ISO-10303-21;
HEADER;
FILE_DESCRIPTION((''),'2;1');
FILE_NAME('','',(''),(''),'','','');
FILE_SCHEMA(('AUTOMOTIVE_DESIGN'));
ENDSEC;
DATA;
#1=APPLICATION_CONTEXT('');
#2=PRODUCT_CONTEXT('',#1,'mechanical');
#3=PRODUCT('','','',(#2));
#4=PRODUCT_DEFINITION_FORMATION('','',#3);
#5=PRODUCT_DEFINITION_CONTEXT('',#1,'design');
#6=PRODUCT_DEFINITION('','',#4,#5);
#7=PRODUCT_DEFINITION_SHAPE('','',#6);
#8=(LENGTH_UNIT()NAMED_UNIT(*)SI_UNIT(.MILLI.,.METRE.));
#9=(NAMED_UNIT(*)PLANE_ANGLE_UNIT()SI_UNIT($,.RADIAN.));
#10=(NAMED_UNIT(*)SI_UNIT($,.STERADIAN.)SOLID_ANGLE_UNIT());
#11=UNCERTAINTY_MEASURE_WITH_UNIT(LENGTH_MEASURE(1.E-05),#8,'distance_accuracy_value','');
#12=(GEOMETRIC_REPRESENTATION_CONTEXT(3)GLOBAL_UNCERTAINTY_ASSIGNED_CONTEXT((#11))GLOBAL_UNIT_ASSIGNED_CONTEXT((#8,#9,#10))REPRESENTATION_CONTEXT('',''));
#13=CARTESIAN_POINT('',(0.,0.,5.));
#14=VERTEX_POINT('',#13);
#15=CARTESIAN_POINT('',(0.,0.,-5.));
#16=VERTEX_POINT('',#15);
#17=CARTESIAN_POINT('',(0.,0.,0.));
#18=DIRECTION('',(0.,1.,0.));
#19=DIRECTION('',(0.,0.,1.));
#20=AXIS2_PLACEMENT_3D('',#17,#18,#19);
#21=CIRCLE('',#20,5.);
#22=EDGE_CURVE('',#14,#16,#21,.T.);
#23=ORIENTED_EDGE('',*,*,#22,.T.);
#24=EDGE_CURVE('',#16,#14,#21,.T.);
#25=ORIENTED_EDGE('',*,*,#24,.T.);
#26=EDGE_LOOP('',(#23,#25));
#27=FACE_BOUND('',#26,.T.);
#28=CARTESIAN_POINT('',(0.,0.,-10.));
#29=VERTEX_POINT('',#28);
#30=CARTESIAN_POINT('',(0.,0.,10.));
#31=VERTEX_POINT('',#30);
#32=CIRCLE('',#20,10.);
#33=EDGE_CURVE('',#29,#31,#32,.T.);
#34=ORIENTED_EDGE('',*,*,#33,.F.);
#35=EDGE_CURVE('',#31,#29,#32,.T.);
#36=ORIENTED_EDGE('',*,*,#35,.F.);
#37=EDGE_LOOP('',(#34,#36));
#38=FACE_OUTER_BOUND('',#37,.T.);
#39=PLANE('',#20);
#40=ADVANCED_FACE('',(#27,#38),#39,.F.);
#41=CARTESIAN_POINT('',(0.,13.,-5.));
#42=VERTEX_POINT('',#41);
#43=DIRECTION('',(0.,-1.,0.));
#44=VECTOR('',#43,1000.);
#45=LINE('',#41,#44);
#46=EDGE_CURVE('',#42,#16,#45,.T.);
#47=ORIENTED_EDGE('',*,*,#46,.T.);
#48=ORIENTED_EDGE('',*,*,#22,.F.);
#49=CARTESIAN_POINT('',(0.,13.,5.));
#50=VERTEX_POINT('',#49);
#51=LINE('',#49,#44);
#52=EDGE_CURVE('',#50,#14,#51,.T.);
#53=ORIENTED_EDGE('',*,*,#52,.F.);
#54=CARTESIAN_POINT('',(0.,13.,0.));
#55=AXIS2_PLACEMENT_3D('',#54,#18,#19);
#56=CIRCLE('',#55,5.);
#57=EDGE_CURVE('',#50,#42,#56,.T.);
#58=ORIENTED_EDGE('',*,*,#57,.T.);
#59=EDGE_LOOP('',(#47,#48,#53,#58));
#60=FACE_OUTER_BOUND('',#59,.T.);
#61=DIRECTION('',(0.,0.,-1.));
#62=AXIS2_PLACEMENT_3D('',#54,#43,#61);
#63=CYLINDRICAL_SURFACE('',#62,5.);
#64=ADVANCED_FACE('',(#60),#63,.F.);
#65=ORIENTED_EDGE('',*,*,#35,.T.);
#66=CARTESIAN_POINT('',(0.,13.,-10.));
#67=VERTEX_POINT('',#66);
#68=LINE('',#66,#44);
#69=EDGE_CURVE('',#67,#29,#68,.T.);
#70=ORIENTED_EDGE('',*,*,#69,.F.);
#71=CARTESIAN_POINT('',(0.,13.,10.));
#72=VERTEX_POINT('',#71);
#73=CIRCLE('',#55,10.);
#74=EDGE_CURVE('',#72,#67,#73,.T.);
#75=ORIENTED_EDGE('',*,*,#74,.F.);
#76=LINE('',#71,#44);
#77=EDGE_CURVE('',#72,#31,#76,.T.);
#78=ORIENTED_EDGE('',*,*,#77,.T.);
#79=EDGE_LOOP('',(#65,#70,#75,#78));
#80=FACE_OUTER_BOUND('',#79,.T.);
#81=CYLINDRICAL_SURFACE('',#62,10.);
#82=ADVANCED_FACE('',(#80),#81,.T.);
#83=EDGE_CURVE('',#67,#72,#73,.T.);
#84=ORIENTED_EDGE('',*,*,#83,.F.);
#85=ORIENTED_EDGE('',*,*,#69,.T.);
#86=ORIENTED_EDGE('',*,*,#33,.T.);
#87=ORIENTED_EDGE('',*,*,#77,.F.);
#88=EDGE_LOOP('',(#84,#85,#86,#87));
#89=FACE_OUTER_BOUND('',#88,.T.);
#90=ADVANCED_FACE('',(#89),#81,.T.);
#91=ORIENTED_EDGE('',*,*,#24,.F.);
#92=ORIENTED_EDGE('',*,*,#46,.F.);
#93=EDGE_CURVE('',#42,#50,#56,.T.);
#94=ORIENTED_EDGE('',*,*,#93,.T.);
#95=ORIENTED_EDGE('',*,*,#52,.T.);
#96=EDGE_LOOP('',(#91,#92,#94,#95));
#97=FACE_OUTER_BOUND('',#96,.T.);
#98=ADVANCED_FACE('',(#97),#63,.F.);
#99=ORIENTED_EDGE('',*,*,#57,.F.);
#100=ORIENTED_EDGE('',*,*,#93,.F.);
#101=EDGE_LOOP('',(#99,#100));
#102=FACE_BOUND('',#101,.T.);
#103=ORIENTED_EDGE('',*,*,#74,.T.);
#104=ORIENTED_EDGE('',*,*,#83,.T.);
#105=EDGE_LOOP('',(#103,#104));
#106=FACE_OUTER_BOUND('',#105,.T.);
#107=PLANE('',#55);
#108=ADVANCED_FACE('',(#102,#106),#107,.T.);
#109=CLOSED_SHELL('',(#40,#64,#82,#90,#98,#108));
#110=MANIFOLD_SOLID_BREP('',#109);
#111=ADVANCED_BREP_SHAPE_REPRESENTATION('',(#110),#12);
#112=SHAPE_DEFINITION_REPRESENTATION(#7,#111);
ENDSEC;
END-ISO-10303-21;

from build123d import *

# Parameters (mm, degrees)
SKETCH1_R           = 10
SKETCH1_R_2         = 5
BOSS_EXTRUDE1_DEPTH = 13


with BuildPart() as part:
    # Sketch1 → Boss-Extrude1 (new body)
    with BuildSketch(Plane(origin=(0, 0, 0), x_dir=(1, 0, 0), z_dir=(0, 1, 0))):
        with Locations(Location((0, 0, 0), (0, 0, 90))):
            Circle(SKETCH1_R)
        with Locations(Location((0, 0, 0), (0, 0, 90))):
            Circle(SKETCH1_R_2, mode=Mode.SUBTRACT)
    extrude(amount=BOSS_EXTRUDE1_DEPTH)


solid = part.part
